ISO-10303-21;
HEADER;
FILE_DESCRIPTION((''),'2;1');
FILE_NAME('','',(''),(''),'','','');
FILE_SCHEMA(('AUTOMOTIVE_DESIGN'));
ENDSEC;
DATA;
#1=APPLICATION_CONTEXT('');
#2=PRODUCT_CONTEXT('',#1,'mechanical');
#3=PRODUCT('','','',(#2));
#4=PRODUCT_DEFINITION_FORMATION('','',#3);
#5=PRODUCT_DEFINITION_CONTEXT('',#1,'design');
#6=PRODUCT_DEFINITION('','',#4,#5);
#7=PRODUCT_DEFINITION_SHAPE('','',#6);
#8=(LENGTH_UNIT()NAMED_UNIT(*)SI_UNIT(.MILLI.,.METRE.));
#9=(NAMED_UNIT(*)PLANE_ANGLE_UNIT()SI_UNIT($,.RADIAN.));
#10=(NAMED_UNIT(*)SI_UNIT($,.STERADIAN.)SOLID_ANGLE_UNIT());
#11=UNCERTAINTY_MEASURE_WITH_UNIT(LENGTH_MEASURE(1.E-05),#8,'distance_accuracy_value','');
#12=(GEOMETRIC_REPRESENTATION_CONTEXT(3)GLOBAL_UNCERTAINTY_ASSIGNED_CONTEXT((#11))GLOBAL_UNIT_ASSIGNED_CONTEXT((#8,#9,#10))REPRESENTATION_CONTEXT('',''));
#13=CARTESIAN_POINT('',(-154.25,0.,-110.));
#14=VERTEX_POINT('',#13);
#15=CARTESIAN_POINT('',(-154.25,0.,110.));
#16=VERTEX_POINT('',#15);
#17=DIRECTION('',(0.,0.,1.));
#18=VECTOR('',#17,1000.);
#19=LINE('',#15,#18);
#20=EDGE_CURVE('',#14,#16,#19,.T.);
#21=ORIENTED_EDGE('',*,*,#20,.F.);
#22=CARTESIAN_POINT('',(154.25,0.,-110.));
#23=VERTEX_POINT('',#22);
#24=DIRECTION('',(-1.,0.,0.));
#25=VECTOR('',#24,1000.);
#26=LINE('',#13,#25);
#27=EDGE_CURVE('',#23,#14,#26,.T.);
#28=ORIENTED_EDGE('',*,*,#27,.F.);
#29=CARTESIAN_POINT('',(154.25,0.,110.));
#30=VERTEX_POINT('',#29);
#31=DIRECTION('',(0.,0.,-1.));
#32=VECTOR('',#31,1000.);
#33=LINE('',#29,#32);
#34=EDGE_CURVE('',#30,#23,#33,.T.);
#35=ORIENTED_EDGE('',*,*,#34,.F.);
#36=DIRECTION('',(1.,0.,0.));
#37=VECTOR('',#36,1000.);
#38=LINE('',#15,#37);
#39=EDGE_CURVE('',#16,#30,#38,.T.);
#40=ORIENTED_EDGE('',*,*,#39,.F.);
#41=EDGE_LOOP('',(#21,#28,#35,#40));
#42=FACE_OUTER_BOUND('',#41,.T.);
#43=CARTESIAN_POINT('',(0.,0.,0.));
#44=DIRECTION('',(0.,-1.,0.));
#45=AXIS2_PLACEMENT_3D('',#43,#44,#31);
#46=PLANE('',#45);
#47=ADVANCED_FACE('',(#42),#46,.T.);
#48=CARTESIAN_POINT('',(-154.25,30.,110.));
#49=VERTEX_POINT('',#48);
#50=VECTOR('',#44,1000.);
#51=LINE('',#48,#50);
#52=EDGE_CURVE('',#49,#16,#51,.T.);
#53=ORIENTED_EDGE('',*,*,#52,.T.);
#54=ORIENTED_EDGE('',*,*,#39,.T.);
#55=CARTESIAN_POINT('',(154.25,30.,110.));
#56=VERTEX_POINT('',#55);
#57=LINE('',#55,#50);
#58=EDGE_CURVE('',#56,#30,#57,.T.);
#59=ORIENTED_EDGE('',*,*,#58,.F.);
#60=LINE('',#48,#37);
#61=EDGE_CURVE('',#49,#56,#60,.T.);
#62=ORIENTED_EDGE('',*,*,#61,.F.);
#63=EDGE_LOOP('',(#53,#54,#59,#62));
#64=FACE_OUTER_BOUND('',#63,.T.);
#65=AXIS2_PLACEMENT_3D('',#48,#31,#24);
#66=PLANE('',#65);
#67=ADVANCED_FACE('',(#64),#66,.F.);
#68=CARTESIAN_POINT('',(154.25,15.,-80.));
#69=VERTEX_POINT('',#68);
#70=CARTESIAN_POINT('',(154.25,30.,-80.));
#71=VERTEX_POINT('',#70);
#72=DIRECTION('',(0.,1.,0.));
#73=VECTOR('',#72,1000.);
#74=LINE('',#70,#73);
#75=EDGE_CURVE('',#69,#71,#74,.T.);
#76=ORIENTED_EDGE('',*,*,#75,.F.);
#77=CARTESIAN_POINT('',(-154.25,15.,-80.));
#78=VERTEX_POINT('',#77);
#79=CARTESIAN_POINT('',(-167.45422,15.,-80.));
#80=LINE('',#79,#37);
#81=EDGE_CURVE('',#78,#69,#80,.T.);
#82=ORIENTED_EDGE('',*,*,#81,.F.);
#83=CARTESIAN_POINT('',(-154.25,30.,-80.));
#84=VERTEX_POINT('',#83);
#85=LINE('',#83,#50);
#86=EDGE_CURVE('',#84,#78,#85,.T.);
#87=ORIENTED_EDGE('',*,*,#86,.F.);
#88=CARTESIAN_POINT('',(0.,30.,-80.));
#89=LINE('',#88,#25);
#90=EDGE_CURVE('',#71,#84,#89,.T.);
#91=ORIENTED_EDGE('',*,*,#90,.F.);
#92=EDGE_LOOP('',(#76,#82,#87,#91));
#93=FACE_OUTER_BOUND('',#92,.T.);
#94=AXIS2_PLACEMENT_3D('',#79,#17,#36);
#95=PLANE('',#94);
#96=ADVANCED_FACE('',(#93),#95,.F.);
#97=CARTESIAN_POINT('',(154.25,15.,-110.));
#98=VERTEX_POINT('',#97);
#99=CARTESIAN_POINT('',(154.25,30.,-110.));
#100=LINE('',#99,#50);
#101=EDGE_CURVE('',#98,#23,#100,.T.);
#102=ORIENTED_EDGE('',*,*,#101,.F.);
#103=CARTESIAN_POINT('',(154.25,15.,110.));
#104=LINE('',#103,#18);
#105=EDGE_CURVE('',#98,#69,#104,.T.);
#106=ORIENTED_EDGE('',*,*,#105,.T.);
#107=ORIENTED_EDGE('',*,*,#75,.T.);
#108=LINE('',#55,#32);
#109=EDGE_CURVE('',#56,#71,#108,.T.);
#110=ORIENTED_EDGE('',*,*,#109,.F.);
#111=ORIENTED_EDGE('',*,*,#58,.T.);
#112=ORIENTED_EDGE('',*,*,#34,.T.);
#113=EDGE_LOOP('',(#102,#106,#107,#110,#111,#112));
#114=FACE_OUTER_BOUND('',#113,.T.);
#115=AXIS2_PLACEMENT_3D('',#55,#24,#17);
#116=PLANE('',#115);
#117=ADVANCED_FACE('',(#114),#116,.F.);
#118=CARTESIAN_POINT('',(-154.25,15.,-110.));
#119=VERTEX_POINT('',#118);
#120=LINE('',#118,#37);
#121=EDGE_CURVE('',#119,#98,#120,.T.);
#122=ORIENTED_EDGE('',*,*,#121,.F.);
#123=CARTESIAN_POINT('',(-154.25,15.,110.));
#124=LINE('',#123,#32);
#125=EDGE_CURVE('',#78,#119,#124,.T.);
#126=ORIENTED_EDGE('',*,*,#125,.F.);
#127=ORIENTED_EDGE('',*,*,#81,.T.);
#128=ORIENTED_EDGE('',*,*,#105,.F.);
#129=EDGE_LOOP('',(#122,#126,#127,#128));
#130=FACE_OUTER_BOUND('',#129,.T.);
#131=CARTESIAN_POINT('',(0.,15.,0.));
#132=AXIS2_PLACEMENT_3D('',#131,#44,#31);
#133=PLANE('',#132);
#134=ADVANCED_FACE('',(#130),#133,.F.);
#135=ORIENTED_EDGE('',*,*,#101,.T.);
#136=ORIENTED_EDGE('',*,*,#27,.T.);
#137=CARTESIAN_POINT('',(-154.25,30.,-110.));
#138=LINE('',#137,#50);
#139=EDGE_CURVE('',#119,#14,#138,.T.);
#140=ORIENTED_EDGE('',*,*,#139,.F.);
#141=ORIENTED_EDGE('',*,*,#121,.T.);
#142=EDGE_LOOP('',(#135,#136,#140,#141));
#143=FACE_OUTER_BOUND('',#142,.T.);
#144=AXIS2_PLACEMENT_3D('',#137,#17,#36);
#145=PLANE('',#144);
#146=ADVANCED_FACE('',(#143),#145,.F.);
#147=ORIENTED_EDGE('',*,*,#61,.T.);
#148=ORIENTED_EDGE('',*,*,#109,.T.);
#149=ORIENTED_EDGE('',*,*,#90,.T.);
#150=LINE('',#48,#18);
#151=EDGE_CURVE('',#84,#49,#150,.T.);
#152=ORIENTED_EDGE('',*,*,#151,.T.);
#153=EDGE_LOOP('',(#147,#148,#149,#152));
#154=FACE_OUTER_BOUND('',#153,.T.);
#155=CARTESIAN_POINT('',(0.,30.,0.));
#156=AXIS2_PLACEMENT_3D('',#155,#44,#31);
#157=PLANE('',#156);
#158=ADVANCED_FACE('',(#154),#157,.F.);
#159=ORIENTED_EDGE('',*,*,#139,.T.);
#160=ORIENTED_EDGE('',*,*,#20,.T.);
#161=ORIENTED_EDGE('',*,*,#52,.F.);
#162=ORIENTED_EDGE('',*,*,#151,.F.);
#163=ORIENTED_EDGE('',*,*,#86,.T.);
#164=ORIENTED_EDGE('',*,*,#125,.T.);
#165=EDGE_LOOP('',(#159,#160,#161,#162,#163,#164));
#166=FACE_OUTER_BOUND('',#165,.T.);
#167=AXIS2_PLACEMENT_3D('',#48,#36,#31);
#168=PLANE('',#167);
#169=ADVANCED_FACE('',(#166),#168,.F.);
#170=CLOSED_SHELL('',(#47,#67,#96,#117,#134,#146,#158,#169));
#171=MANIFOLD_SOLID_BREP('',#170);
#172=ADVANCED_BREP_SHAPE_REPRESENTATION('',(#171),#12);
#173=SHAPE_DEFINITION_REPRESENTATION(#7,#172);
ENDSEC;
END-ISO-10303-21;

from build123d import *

# Parameters (mm, degrees)
SKETCH_1_W          = 308.5
SKETCH_1_H          = 220
EXTRUDE_1_DEPTH     = 30
SKETCH_2_W          = 366.462982974
SKETCH_2_H          = 68.169207718
CUT_EXTRUDE_1_DEPTH = 15


with BuildPart() as part:
    # 草图1 → 凸台-拉伸1 (new body)
    with BuildSketch(Plane(origin=(0, 0, 0), x_dir=(1, 0, 0), z_dir=(0, 1, 0))):
        Rectangle(SKETCH_1_W, SKETCH_1_H)
    extrude(amount=EXTRUDE_1_DEPTH)

    # 草图2 → 切除-拉伸1 (cut)
    with BuildSketch(Plane(origin=(0, 30, 0), x_dir=(1, 0, 0), z_dir=(0, 1, 0))):
        with Locations((15.777271283, 114.084603859)):
            Rectangle(SKETCH_2_W, SKETCH_2_H)
    extrude(amount=-CUT_EXTRUDE_1_DEPTH, mode=Mode.SUBTRACT)


solid = part.part
